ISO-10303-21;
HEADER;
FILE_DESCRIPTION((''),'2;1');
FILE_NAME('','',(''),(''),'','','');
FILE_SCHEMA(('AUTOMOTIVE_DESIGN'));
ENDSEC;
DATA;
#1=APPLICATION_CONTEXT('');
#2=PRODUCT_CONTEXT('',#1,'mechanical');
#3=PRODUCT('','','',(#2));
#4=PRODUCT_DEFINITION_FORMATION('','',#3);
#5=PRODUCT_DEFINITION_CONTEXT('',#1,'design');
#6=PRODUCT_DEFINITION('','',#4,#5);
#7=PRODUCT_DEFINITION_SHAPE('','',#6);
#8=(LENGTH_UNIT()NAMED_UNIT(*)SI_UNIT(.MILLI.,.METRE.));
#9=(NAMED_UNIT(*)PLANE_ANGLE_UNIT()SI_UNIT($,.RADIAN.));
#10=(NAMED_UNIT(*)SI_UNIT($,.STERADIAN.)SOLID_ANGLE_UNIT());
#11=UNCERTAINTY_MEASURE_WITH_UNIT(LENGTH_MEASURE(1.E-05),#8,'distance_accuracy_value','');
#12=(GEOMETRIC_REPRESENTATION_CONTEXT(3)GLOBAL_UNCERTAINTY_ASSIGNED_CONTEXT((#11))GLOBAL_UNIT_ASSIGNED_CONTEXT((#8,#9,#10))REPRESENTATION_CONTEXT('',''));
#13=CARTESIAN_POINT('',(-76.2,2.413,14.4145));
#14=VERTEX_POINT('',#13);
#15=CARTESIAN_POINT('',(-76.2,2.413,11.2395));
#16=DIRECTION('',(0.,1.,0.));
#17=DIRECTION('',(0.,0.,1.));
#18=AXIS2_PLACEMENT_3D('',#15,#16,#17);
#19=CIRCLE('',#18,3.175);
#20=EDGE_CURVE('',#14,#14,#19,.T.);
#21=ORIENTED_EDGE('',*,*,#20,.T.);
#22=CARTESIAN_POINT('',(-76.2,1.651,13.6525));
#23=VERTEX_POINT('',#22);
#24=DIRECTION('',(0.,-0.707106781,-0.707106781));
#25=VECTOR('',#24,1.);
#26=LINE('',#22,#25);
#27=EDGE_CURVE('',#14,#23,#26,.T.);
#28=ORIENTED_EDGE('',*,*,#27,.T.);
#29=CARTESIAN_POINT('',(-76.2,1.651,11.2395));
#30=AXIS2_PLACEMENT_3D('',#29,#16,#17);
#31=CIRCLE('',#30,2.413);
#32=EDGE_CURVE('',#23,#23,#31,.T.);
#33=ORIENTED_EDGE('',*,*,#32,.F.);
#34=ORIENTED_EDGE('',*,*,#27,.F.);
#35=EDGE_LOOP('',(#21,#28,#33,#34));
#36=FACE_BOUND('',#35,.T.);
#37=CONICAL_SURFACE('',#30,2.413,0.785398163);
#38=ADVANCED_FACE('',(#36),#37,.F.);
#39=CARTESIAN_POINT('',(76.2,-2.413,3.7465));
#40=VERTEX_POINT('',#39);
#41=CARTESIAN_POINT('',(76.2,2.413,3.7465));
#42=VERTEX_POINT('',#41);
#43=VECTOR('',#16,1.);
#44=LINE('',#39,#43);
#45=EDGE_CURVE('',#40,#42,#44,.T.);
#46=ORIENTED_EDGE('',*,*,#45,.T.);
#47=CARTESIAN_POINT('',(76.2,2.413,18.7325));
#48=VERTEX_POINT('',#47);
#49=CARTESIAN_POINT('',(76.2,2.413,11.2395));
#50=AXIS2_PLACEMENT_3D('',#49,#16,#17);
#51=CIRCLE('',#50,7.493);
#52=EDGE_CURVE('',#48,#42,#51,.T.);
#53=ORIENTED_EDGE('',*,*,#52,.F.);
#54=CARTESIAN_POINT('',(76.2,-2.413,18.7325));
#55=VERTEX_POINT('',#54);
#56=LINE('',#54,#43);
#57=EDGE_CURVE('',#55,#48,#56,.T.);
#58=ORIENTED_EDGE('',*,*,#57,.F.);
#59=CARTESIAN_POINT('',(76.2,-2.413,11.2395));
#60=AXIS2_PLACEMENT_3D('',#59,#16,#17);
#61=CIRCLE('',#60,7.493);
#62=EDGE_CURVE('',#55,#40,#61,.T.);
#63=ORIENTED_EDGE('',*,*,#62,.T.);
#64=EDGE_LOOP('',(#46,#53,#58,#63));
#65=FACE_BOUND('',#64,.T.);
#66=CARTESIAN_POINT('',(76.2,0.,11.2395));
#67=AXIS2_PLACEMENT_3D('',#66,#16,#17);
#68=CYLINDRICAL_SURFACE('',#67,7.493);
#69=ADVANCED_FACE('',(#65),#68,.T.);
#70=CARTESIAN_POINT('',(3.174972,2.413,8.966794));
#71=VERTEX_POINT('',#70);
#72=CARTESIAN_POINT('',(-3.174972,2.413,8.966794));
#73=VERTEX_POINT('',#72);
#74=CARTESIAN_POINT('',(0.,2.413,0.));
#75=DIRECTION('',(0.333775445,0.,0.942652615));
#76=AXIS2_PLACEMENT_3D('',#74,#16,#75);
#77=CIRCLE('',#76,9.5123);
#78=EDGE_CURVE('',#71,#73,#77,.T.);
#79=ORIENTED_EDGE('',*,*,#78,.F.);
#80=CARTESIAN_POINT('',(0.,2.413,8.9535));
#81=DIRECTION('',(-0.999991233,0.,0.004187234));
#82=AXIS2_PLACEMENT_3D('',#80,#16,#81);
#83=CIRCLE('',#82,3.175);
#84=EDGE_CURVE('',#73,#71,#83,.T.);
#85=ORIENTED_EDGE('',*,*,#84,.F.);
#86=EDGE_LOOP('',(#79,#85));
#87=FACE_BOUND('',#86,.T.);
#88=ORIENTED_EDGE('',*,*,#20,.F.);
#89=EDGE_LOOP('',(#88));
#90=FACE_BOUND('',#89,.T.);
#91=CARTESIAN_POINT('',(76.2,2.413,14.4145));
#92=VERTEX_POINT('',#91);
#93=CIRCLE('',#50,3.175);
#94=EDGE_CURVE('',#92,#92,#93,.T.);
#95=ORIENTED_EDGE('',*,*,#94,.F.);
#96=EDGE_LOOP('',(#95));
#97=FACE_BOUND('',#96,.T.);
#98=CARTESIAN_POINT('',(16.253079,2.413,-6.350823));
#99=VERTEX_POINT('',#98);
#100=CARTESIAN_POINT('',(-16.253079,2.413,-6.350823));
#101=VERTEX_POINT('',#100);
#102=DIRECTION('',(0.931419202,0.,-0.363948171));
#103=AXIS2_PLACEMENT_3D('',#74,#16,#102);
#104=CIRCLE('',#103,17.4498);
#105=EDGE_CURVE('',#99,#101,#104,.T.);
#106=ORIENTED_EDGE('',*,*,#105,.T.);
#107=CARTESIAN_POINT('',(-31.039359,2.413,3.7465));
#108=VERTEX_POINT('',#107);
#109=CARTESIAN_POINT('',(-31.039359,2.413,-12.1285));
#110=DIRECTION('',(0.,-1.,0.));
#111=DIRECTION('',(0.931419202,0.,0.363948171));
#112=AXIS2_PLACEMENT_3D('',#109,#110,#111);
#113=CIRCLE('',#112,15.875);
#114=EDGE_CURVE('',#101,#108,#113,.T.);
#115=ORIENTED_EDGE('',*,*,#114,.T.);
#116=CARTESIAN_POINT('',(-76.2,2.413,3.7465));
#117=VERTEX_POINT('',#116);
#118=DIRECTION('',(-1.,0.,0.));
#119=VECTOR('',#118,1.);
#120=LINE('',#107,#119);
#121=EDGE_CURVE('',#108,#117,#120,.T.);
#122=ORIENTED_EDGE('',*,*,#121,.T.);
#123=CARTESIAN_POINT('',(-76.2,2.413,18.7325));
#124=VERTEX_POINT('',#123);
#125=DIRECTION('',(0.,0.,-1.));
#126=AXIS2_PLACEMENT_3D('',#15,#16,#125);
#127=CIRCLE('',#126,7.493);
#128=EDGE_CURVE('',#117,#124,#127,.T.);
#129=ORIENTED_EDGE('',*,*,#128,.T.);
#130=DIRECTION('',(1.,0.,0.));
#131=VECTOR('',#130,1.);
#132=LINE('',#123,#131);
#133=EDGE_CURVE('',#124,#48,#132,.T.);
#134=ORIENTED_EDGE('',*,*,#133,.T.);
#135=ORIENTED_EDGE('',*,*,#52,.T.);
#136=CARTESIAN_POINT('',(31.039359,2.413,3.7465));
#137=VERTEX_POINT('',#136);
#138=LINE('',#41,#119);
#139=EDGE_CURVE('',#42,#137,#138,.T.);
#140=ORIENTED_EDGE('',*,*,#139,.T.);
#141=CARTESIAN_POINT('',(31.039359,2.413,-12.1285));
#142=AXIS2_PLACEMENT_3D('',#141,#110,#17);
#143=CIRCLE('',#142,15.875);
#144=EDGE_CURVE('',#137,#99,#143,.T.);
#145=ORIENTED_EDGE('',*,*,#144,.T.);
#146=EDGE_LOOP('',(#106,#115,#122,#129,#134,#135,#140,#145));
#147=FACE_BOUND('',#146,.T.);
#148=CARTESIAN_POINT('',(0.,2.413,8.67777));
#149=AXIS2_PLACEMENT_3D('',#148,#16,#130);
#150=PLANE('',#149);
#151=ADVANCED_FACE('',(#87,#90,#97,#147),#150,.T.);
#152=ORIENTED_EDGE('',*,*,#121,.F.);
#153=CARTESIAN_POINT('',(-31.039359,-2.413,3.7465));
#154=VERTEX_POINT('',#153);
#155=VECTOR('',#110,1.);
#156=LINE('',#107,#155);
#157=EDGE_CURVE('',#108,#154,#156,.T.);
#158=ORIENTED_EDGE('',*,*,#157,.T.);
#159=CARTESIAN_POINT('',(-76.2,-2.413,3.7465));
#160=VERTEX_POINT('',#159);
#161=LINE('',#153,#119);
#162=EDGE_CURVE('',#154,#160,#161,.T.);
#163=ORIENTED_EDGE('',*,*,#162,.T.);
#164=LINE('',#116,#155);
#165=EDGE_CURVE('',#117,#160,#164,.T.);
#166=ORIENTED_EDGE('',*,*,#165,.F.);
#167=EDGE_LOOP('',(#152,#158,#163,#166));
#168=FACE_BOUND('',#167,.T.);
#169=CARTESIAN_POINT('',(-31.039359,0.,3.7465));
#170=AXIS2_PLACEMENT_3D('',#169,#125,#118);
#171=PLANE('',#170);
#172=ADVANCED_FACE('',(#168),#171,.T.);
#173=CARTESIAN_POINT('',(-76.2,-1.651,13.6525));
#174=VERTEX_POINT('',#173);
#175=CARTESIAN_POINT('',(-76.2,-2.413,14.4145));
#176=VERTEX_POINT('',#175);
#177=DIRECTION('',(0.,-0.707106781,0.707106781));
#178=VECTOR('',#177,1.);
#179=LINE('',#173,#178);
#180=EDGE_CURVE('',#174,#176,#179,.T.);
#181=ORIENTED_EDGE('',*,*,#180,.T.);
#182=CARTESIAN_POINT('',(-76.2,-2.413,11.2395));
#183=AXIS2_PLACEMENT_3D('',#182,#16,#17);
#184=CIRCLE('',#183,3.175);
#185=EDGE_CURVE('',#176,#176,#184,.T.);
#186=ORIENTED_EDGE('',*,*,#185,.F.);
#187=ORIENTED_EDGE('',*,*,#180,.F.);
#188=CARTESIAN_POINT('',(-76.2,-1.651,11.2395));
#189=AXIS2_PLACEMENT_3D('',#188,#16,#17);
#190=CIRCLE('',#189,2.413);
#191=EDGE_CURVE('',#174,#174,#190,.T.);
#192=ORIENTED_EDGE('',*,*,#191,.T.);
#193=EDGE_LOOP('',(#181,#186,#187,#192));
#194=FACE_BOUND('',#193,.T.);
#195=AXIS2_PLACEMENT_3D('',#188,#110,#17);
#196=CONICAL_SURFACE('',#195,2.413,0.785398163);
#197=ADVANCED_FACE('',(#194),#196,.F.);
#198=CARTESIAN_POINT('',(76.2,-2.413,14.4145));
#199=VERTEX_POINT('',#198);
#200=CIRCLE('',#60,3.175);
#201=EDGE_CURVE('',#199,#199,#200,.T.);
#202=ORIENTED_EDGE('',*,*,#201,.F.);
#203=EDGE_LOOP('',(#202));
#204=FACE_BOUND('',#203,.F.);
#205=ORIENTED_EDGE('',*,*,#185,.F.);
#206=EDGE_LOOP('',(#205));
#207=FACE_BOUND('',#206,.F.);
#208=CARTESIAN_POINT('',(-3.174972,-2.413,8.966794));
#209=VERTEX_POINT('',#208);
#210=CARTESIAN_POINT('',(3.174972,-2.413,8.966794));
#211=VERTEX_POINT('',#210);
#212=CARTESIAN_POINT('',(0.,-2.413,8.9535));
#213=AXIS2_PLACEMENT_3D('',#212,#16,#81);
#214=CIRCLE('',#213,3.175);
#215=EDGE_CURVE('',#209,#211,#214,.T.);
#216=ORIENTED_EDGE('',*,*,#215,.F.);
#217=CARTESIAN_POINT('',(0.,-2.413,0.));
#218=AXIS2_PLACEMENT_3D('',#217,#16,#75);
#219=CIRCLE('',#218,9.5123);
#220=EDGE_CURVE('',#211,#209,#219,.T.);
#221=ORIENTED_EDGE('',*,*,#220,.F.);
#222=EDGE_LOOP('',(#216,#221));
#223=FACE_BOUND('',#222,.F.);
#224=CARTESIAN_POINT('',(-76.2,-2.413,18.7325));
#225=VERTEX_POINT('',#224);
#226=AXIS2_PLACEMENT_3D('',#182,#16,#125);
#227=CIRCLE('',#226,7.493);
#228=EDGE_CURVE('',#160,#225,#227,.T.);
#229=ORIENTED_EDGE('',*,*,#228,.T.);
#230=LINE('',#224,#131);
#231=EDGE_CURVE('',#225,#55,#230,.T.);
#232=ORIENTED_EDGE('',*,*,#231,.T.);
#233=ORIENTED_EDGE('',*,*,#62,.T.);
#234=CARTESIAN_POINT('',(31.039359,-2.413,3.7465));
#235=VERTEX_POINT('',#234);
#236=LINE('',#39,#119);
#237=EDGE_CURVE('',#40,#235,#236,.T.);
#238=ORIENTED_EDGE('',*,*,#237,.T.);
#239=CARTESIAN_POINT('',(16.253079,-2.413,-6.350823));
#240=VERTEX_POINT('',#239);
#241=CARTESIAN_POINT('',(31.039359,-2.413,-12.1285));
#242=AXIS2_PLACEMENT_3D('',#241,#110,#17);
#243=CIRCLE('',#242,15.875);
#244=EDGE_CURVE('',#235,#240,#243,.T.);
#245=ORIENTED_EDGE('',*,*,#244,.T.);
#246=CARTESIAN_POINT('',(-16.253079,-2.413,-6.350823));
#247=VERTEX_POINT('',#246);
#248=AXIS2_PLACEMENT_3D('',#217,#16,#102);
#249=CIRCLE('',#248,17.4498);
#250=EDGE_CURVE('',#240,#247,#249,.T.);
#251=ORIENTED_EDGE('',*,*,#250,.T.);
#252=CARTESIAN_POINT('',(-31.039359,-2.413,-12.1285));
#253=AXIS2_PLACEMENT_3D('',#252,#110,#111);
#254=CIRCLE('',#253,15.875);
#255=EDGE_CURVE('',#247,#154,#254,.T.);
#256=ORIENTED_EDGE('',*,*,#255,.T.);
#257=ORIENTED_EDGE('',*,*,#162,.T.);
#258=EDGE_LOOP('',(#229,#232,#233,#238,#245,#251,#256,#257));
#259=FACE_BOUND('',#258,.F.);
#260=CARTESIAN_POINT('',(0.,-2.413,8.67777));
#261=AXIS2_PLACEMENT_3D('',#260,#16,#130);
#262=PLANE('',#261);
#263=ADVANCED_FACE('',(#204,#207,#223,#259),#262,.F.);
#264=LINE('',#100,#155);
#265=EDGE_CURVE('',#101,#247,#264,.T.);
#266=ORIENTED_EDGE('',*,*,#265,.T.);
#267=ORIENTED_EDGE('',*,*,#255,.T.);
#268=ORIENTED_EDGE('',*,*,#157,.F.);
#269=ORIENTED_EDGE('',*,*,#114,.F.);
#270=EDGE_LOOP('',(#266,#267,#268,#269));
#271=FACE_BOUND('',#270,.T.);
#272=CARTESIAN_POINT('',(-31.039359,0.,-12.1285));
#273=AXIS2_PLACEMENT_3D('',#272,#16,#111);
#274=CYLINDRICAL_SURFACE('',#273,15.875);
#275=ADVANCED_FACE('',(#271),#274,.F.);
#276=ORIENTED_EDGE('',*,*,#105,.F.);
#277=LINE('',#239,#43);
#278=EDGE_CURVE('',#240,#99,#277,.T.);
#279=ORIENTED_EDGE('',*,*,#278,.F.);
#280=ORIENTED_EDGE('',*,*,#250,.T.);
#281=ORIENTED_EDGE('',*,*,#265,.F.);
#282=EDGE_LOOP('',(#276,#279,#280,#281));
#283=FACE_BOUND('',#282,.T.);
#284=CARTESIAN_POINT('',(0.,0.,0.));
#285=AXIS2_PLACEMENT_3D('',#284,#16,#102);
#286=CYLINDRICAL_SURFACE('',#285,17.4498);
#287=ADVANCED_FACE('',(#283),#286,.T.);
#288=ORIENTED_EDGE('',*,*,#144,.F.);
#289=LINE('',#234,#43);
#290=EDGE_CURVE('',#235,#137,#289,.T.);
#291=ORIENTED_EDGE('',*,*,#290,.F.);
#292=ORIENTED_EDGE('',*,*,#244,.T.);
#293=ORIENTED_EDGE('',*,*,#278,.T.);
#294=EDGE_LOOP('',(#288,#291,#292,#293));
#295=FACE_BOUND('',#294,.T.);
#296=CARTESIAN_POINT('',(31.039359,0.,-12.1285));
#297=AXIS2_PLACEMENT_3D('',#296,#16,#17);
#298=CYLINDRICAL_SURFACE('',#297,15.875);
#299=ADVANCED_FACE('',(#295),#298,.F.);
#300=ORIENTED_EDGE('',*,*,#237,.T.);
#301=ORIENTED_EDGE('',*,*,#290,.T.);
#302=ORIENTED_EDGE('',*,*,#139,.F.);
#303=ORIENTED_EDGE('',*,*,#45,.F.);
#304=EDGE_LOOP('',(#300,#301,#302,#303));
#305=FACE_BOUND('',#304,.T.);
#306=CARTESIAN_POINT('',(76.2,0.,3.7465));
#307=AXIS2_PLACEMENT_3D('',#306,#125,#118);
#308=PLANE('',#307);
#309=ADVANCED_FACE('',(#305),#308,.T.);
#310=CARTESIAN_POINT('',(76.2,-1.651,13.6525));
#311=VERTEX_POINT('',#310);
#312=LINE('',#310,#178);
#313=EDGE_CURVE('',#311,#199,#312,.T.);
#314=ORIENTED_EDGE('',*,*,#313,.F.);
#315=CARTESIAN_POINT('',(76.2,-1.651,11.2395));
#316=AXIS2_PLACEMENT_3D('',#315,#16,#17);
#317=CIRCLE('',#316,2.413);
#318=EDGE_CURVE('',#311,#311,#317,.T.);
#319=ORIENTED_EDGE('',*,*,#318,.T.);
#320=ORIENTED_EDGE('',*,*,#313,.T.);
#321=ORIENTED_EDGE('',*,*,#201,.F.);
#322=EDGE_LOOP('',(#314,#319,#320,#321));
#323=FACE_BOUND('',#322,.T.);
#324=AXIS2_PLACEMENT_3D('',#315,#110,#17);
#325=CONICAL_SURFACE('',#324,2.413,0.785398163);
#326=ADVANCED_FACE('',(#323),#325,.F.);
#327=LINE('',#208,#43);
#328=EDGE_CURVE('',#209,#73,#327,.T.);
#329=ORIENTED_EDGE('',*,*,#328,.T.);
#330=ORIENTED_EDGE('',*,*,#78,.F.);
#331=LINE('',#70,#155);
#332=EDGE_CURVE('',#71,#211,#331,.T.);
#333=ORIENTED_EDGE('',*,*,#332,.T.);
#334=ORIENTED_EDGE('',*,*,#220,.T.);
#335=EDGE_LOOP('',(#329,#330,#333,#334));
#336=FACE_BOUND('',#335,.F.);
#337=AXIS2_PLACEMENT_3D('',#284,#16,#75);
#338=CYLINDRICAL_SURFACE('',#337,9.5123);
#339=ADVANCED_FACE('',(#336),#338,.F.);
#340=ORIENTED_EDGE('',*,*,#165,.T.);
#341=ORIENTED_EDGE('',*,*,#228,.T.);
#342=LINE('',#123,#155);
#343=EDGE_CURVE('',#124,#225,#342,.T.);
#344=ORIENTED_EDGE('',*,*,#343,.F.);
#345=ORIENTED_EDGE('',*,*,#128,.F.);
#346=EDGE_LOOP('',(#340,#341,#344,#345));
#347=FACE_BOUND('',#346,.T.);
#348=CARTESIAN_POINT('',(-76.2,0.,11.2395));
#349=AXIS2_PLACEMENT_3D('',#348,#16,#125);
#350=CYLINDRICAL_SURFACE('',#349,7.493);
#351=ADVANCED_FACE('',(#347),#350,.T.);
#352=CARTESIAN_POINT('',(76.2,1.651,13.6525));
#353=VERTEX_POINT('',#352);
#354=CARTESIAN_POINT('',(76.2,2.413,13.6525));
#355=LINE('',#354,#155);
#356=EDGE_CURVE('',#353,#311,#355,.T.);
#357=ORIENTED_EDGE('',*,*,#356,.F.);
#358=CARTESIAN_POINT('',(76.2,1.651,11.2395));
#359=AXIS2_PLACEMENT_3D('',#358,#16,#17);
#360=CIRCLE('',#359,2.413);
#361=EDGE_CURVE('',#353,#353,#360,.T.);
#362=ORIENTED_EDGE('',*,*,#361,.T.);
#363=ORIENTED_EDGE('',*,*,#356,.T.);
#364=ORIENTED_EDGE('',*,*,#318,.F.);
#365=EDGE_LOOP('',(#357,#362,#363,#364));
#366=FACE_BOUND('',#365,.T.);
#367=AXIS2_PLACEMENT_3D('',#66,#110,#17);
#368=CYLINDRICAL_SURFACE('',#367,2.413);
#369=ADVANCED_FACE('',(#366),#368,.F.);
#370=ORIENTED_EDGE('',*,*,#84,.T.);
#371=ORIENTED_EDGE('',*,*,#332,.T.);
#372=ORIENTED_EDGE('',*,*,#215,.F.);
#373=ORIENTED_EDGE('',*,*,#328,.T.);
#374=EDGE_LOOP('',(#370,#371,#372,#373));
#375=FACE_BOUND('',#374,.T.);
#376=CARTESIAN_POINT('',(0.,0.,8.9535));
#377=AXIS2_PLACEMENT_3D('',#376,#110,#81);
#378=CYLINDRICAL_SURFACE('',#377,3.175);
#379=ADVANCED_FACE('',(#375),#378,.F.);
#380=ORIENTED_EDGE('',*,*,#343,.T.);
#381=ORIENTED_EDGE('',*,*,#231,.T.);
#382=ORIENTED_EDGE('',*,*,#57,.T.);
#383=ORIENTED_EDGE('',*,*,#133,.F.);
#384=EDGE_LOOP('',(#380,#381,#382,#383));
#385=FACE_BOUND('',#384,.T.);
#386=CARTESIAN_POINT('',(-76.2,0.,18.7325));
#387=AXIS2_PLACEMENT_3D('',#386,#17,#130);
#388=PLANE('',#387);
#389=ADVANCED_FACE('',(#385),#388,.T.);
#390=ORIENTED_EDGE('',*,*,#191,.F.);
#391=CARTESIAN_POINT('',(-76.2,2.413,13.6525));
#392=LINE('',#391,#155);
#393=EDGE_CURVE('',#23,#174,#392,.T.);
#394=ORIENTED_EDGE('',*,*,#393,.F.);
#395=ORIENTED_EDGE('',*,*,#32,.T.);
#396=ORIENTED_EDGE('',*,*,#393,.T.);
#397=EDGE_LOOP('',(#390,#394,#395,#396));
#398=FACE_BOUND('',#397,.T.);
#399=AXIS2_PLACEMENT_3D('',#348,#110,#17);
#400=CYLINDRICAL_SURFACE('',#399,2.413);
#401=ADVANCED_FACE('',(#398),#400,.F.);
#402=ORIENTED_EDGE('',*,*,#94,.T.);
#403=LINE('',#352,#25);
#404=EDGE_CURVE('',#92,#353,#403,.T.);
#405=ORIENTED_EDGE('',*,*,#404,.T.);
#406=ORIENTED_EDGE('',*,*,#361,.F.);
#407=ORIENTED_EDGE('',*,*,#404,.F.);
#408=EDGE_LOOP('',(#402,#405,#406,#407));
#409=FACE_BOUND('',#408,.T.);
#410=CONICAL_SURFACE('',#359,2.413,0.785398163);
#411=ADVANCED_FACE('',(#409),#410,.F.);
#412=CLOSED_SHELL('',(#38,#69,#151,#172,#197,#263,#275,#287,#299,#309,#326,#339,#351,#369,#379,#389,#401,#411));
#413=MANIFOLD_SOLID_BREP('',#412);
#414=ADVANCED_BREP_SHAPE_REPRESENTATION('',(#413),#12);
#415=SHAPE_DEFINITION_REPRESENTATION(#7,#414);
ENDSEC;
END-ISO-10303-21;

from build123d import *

# Parameters (mm, degrees)
SKETCH1_R           = 2.413
BOSS_EXTRUDE1_DEPTH = 2.413
CHAMFER1_SIZE       = 0.762


with BuildPart() as part:
    # Sketch1 → Boss-Extrude1 (new, symmetric)
    with BuildSketch(Plane(origin=(0, 0, 0), x_dir=(1, 0, 0), z_dir=(0, 1, 0))):
        with BuildLine():
            Line((-76.2, -18.7325), (76.2, -18.7325))
            ThreePointArc((76.2, -18.7325), (83.693, -11.2395), (76.2, -3.7465))
            Line((76.2, -3.7465), (31.039358608, -3.7465))
            ThreePointArc((31.039358608, -3.7465), (22.086845014, -0.981348411), (16.253078783, 6.35082279))
            ThreePointArc((16.253078783, 6.35082279), (0, 17.4498), (-16.253078783, 6.35082279))
            ThreePointArc((-16.253078783, 6.35082279), (-22.086845014, -0.981348411), (-31.039358608, -3.7465))
            Line((-31.039358608, -3.7465), (-76.2, -3.7465))
            ThreePointArc((-76.2, -3.7465), (-83.693, -11.2395), (-76.2, -18.7325))
        make_face()
        with Locations(Location((76.2, -11.2395, 0), (0, 0, 270))):
            Circle(SKETCH1_R, mode=Mode.SUBTRACT)
        with Locations(Location((-76.2, -11.2395, 0), (0, 0, 270))):
            Circle(SKETCH1_R, mode=Mode.SUBTRACT)
        with BuildLine():
            ThreePointArc((3.174972166, -8.966794468), (0, 9.5123), (-3.174972166, -8.966794468))
            ThreePointArc((-3.174972166, -8.966794468), (0, -12.1285), (3.174972166, -8.966794468))
        make_face(mode=Mode.SUBTRACT)
    extrude(amount=BOSS_EXTRUDE1_DEPTH, both=True)

    # Chamfer1
    chamfer1_edges = [part.edges().sort_by_distance(p)[0] for p in [
        (76.2, -2.413, 8.8265),
        (76.2, 2.413, 8.8265),
        (-76.2, -2.413, 8.8265),
        (-76.2, 2.413, 8.8265),
    ]]
    chamfer(chamfer1_edges, length=CHAMFER1_SIZE)


solid = part.part
